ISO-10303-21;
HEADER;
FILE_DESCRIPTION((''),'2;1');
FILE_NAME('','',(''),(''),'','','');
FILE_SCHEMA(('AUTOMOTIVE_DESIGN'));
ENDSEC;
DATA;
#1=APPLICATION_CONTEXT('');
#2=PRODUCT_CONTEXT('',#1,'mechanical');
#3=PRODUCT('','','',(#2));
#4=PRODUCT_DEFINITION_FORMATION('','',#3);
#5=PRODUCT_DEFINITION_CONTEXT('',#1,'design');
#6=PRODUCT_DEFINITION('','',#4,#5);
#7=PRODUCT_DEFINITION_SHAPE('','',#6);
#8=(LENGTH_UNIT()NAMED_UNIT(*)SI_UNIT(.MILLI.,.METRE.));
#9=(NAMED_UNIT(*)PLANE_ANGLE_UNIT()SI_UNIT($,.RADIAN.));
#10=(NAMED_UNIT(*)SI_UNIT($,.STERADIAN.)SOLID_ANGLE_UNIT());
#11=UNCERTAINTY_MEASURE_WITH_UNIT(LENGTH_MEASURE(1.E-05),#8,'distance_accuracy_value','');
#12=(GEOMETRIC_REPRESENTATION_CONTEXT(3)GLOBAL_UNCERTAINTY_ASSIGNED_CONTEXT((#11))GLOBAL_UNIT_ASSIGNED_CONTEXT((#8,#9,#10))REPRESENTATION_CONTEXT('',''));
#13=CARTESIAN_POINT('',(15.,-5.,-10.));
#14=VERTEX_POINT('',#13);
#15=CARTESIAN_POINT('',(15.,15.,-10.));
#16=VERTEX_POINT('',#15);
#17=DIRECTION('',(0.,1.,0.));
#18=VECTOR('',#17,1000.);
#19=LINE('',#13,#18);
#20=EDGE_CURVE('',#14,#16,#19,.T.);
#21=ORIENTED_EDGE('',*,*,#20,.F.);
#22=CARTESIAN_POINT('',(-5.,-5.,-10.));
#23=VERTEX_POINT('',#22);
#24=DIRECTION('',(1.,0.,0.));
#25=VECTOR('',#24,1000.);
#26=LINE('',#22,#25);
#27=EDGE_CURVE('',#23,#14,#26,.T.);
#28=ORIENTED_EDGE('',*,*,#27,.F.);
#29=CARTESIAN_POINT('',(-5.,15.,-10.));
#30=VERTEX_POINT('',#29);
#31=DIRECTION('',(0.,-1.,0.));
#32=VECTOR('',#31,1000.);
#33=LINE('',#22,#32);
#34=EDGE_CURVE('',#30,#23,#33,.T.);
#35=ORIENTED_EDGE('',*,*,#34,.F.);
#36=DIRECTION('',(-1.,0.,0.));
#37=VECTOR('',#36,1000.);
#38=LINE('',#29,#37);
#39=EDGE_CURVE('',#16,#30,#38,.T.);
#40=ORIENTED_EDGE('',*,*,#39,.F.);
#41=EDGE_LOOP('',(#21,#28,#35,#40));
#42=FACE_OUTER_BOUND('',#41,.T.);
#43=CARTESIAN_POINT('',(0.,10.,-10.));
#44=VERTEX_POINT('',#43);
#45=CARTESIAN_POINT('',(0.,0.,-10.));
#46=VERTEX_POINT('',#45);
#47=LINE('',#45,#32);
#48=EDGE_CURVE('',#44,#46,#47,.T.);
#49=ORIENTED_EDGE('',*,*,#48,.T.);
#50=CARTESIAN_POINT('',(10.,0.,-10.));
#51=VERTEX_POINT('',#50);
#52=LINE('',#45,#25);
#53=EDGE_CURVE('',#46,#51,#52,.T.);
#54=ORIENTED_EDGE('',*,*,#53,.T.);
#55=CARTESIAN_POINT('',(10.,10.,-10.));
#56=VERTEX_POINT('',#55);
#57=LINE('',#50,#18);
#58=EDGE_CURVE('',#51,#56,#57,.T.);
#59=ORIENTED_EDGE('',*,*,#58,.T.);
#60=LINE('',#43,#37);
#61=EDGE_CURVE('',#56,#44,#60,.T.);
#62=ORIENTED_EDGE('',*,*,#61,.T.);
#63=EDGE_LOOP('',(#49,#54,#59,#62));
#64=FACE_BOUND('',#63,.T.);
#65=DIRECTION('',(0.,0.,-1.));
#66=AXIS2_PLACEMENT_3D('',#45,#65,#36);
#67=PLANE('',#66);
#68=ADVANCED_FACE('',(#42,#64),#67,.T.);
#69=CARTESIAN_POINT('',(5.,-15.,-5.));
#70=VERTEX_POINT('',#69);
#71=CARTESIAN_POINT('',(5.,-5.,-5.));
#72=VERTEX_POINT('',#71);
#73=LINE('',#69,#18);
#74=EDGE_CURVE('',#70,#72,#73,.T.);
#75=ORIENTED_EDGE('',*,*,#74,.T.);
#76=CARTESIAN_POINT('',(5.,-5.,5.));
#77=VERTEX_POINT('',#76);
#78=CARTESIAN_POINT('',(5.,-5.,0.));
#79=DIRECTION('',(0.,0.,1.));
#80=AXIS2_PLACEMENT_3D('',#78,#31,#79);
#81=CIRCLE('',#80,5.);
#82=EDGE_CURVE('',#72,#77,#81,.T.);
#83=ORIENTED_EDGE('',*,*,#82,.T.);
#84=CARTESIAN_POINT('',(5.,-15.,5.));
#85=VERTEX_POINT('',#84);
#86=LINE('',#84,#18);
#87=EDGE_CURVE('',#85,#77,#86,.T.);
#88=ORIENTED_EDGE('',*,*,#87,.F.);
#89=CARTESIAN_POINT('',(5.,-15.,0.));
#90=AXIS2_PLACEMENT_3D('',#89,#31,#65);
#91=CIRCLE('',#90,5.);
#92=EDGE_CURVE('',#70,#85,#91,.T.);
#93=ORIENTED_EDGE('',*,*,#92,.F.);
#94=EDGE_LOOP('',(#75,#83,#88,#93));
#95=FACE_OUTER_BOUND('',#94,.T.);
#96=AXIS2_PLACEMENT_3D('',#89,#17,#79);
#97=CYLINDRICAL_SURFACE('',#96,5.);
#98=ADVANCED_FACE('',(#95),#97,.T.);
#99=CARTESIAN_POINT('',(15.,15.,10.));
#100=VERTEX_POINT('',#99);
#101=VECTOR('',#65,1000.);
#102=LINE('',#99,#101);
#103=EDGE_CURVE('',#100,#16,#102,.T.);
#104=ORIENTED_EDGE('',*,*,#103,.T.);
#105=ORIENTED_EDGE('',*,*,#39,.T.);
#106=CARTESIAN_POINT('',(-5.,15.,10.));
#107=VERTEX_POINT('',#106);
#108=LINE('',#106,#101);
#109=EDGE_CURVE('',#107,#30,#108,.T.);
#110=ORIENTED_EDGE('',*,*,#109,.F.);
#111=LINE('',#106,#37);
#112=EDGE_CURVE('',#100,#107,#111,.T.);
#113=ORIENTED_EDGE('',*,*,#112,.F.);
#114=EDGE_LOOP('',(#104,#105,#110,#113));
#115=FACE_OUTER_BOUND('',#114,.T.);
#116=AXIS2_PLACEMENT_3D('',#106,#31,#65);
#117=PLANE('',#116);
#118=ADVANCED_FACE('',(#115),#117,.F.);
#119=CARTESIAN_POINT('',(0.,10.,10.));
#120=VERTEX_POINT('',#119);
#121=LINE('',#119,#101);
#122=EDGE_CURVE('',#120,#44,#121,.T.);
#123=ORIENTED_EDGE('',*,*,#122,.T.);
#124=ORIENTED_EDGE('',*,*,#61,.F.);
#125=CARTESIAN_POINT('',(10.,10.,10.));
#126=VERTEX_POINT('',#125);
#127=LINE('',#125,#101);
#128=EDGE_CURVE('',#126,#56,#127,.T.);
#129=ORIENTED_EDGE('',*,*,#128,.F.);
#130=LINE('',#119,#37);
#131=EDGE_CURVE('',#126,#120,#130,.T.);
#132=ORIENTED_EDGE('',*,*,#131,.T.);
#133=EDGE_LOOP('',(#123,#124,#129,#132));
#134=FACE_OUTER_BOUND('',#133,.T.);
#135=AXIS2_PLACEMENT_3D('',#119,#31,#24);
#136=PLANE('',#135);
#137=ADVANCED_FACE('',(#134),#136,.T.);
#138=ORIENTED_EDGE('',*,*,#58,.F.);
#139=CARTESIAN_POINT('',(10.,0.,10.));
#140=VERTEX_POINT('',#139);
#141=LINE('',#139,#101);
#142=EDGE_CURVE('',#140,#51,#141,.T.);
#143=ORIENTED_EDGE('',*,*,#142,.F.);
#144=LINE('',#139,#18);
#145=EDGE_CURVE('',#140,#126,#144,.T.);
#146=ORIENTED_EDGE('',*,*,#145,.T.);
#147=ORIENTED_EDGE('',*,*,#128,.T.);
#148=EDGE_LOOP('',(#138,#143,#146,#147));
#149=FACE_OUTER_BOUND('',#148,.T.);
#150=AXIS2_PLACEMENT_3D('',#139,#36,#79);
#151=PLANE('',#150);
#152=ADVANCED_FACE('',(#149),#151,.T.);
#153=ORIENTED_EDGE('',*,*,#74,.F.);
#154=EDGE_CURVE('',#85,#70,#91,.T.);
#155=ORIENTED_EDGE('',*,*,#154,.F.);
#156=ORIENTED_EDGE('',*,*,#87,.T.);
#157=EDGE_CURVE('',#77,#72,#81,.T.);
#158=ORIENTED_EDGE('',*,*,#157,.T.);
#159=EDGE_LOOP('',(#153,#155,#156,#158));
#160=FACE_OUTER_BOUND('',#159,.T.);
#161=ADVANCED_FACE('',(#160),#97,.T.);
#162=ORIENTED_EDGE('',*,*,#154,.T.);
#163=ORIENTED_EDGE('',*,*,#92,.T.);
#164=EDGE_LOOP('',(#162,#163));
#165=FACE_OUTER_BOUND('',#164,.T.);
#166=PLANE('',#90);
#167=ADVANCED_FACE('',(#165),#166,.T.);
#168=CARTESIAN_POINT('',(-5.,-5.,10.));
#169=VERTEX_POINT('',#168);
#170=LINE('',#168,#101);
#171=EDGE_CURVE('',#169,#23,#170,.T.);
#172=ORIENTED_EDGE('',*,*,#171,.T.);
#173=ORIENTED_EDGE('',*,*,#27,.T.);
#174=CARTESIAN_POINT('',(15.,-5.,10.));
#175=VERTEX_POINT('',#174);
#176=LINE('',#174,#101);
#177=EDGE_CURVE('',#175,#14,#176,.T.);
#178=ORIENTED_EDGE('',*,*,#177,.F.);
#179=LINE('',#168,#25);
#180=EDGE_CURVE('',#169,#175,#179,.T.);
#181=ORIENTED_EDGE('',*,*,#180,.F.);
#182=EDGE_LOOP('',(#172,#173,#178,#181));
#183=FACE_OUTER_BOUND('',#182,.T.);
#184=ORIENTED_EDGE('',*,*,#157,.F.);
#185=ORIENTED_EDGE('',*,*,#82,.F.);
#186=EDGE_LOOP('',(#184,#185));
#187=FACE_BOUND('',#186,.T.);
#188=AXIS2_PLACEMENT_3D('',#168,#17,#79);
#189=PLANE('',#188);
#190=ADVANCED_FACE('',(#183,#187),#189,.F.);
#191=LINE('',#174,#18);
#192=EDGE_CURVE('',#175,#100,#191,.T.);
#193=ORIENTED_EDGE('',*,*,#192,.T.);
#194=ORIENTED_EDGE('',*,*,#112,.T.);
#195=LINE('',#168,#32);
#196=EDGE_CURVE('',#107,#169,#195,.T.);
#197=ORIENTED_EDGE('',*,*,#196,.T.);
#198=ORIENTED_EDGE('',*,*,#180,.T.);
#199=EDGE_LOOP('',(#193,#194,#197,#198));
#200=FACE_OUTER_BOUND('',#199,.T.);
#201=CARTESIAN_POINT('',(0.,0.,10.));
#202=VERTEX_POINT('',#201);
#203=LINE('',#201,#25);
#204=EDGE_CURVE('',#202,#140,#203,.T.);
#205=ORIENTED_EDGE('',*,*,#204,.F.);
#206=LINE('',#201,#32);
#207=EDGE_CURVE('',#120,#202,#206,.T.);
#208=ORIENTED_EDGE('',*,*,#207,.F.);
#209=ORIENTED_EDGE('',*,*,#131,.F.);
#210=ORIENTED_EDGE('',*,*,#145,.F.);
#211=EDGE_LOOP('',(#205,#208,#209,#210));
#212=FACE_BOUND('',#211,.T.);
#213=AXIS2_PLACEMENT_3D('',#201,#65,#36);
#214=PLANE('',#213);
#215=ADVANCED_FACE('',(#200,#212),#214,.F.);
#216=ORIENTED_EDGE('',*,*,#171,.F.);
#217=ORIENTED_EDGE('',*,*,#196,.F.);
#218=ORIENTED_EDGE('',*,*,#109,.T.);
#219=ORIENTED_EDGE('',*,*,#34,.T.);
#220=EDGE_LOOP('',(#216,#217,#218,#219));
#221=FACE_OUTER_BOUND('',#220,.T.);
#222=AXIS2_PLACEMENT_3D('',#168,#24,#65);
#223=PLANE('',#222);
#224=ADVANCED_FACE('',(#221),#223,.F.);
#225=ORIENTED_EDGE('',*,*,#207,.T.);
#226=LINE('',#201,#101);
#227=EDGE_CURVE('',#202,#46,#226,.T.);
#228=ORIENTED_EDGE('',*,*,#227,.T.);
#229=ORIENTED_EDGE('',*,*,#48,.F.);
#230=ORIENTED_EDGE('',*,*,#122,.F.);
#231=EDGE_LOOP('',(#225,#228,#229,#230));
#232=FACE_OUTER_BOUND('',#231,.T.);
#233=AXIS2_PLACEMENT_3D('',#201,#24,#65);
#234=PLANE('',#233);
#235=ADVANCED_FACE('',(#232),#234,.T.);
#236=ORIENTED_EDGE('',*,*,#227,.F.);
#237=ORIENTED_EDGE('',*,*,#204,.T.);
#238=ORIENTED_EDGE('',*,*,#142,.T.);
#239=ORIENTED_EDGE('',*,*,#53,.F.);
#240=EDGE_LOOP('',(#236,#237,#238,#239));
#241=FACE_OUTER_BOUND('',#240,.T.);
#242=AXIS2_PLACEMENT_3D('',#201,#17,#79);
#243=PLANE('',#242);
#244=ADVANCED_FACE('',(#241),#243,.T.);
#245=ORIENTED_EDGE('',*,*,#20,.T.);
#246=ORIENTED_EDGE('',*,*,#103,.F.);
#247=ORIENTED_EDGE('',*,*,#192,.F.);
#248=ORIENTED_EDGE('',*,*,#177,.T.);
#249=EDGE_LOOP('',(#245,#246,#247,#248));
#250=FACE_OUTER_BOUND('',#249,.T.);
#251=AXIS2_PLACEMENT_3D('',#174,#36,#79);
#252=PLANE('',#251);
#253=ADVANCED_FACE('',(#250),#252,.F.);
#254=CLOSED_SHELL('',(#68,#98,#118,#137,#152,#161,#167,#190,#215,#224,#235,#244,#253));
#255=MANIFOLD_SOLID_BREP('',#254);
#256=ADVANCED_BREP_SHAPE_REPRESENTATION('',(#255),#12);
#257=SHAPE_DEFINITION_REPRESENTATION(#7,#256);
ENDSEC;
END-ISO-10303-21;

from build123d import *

# Parameters (mm, degrees)
SKETCH_1_W      = 20
SKETCH_1_H      = 20
SKETCH_1_W_2    = 10
SKETCH_1_H_2    = 10
EXTRUDE_1_DEPTH = 10
SKETCH_2_R      = 5
EXTRUDE_2_DEPTH = 10


with BuildPart() as part:
    # 草图1 → 凸台-拉伸1 (new, symmetric)
    with BuildSketch(Plane.XY):
        with Locations((5, 5)):
            Rectangle(SKETCH_1_W, SKETCH_1_H)
        with Locations((5, 5)):
            Rectangle(SKETCH_1_W_2, SKETCH_1_H_2, mode=Mode.SUBTRACT)
    extrude(amount=EXTRUDE_1_DEPTH, both=True)

    # 草图2 → 凸台-拉伸2 (add)
    with BuildSketch(Plane.XZ.offset(5)):
        with Locations(Location((5, 0, 0), (0, 0, 90))):
            Circle(SKETCH_2_R)
    extrude(amount=EXTRUDE_2_DEPTH)


solid = part.part
